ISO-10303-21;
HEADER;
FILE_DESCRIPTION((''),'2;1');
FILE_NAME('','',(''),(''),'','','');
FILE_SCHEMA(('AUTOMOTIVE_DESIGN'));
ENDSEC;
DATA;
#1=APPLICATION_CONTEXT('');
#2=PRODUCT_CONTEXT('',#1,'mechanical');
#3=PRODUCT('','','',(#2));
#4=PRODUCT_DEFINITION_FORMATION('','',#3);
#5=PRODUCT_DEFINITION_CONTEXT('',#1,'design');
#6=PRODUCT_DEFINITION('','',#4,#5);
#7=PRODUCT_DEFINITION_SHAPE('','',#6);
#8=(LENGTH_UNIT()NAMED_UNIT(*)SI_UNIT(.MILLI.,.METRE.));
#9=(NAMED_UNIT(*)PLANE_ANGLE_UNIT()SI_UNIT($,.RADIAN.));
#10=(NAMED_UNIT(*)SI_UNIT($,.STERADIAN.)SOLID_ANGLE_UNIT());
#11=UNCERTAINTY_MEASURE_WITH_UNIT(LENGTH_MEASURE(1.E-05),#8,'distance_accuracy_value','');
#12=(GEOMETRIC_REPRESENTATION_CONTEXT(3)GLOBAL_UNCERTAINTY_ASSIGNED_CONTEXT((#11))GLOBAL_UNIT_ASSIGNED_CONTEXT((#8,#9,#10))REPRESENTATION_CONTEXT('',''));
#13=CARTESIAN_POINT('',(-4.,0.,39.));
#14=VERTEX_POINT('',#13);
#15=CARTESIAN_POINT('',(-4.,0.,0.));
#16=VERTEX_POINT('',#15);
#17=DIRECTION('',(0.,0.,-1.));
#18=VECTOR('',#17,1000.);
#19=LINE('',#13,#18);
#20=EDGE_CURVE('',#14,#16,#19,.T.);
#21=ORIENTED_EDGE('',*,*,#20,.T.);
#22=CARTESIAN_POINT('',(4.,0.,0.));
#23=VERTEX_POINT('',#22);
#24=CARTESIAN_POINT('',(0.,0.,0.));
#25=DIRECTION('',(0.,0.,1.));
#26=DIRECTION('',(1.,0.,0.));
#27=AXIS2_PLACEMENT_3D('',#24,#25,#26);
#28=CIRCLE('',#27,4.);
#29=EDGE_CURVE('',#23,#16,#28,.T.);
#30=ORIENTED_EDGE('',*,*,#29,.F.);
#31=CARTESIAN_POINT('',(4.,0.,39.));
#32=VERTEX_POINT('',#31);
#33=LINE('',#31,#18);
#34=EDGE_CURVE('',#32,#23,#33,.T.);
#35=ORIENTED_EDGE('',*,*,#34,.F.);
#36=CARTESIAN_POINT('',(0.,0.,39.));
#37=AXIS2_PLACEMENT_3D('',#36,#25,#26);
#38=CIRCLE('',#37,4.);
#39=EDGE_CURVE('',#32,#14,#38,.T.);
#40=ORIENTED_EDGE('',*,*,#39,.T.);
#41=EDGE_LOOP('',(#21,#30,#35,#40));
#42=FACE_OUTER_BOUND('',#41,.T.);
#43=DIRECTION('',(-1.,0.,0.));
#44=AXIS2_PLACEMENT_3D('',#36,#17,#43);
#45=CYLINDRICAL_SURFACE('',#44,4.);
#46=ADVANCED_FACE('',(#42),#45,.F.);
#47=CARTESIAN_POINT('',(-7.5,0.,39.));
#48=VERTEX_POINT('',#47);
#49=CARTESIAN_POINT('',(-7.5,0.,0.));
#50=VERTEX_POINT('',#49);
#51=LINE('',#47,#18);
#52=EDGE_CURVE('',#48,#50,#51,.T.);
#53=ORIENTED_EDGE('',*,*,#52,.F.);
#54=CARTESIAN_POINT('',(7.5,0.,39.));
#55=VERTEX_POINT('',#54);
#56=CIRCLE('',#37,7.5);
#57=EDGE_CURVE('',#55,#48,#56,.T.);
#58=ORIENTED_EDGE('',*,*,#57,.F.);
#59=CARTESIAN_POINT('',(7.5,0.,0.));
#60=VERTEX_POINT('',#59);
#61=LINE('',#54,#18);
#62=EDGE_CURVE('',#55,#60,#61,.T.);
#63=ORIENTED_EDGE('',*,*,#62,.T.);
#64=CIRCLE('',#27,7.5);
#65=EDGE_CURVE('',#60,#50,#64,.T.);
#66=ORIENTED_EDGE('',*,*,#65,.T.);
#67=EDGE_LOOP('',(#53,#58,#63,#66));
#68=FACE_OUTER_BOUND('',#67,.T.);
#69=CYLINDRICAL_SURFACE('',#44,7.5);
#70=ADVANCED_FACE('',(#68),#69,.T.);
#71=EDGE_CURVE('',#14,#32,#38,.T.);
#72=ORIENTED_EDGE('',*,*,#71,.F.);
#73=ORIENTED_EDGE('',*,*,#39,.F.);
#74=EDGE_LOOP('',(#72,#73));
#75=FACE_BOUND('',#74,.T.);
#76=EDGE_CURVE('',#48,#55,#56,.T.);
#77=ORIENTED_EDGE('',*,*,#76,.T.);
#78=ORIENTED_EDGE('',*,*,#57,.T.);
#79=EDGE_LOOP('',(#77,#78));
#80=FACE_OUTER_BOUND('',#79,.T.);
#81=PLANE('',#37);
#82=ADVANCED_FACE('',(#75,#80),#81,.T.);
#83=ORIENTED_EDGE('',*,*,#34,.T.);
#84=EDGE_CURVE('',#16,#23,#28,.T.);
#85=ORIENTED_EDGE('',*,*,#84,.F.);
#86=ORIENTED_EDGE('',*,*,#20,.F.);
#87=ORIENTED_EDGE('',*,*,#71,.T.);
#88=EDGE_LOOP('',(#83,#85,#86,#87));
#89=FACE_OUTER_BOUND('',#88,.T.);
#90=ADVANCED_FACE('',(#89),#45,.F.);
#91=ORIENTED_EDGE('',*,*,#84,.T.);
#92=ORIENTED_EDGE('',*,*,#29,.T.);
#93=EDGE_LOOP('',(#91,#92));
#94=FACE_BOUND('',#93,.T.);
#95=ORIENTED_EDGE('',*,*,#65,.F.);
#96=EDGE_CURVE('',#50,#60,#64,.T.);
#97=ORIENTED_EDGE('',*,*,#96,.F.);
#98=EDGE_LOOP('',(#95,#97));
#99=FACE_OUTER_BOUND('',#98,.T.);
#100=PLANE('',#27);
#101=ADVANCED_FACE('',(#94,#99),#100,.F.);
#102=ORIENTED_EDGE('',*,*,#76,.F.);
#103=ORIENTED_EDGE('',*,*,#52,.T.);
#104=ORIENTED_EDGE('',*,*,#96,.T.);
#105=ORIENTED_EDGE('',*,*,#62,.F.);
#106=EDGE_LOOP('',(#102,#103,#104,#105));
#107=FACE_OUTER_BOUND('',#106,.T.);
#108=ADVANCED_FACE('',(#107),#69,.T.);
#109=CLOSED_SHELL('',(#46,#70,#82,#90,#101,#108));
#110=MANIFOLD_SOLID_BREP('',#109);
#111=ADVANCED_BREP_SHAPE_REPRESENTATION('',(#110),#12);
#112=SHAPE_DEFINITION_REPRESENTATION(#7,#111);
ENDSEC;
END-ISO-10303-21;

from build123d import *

# Parameters (mm, degrees)
SKETCH1_R           = 7.5
SKETCH1_R_2         = 4
BOSS_EXTRUDE1_DEPTH = 39


with BuildPart() as part:
    # Sketch1 → Boss-Extrude1 (new body)
    with BuildSketch(Plane.XY):
        Circle(SKETCH1_R)
        Circle(SKETCH1_R_2, mode=Mode.SUBTRACT)
    extrude(amount=BOSS_EXTRUDE1_DEPTH)


solid = part.part
